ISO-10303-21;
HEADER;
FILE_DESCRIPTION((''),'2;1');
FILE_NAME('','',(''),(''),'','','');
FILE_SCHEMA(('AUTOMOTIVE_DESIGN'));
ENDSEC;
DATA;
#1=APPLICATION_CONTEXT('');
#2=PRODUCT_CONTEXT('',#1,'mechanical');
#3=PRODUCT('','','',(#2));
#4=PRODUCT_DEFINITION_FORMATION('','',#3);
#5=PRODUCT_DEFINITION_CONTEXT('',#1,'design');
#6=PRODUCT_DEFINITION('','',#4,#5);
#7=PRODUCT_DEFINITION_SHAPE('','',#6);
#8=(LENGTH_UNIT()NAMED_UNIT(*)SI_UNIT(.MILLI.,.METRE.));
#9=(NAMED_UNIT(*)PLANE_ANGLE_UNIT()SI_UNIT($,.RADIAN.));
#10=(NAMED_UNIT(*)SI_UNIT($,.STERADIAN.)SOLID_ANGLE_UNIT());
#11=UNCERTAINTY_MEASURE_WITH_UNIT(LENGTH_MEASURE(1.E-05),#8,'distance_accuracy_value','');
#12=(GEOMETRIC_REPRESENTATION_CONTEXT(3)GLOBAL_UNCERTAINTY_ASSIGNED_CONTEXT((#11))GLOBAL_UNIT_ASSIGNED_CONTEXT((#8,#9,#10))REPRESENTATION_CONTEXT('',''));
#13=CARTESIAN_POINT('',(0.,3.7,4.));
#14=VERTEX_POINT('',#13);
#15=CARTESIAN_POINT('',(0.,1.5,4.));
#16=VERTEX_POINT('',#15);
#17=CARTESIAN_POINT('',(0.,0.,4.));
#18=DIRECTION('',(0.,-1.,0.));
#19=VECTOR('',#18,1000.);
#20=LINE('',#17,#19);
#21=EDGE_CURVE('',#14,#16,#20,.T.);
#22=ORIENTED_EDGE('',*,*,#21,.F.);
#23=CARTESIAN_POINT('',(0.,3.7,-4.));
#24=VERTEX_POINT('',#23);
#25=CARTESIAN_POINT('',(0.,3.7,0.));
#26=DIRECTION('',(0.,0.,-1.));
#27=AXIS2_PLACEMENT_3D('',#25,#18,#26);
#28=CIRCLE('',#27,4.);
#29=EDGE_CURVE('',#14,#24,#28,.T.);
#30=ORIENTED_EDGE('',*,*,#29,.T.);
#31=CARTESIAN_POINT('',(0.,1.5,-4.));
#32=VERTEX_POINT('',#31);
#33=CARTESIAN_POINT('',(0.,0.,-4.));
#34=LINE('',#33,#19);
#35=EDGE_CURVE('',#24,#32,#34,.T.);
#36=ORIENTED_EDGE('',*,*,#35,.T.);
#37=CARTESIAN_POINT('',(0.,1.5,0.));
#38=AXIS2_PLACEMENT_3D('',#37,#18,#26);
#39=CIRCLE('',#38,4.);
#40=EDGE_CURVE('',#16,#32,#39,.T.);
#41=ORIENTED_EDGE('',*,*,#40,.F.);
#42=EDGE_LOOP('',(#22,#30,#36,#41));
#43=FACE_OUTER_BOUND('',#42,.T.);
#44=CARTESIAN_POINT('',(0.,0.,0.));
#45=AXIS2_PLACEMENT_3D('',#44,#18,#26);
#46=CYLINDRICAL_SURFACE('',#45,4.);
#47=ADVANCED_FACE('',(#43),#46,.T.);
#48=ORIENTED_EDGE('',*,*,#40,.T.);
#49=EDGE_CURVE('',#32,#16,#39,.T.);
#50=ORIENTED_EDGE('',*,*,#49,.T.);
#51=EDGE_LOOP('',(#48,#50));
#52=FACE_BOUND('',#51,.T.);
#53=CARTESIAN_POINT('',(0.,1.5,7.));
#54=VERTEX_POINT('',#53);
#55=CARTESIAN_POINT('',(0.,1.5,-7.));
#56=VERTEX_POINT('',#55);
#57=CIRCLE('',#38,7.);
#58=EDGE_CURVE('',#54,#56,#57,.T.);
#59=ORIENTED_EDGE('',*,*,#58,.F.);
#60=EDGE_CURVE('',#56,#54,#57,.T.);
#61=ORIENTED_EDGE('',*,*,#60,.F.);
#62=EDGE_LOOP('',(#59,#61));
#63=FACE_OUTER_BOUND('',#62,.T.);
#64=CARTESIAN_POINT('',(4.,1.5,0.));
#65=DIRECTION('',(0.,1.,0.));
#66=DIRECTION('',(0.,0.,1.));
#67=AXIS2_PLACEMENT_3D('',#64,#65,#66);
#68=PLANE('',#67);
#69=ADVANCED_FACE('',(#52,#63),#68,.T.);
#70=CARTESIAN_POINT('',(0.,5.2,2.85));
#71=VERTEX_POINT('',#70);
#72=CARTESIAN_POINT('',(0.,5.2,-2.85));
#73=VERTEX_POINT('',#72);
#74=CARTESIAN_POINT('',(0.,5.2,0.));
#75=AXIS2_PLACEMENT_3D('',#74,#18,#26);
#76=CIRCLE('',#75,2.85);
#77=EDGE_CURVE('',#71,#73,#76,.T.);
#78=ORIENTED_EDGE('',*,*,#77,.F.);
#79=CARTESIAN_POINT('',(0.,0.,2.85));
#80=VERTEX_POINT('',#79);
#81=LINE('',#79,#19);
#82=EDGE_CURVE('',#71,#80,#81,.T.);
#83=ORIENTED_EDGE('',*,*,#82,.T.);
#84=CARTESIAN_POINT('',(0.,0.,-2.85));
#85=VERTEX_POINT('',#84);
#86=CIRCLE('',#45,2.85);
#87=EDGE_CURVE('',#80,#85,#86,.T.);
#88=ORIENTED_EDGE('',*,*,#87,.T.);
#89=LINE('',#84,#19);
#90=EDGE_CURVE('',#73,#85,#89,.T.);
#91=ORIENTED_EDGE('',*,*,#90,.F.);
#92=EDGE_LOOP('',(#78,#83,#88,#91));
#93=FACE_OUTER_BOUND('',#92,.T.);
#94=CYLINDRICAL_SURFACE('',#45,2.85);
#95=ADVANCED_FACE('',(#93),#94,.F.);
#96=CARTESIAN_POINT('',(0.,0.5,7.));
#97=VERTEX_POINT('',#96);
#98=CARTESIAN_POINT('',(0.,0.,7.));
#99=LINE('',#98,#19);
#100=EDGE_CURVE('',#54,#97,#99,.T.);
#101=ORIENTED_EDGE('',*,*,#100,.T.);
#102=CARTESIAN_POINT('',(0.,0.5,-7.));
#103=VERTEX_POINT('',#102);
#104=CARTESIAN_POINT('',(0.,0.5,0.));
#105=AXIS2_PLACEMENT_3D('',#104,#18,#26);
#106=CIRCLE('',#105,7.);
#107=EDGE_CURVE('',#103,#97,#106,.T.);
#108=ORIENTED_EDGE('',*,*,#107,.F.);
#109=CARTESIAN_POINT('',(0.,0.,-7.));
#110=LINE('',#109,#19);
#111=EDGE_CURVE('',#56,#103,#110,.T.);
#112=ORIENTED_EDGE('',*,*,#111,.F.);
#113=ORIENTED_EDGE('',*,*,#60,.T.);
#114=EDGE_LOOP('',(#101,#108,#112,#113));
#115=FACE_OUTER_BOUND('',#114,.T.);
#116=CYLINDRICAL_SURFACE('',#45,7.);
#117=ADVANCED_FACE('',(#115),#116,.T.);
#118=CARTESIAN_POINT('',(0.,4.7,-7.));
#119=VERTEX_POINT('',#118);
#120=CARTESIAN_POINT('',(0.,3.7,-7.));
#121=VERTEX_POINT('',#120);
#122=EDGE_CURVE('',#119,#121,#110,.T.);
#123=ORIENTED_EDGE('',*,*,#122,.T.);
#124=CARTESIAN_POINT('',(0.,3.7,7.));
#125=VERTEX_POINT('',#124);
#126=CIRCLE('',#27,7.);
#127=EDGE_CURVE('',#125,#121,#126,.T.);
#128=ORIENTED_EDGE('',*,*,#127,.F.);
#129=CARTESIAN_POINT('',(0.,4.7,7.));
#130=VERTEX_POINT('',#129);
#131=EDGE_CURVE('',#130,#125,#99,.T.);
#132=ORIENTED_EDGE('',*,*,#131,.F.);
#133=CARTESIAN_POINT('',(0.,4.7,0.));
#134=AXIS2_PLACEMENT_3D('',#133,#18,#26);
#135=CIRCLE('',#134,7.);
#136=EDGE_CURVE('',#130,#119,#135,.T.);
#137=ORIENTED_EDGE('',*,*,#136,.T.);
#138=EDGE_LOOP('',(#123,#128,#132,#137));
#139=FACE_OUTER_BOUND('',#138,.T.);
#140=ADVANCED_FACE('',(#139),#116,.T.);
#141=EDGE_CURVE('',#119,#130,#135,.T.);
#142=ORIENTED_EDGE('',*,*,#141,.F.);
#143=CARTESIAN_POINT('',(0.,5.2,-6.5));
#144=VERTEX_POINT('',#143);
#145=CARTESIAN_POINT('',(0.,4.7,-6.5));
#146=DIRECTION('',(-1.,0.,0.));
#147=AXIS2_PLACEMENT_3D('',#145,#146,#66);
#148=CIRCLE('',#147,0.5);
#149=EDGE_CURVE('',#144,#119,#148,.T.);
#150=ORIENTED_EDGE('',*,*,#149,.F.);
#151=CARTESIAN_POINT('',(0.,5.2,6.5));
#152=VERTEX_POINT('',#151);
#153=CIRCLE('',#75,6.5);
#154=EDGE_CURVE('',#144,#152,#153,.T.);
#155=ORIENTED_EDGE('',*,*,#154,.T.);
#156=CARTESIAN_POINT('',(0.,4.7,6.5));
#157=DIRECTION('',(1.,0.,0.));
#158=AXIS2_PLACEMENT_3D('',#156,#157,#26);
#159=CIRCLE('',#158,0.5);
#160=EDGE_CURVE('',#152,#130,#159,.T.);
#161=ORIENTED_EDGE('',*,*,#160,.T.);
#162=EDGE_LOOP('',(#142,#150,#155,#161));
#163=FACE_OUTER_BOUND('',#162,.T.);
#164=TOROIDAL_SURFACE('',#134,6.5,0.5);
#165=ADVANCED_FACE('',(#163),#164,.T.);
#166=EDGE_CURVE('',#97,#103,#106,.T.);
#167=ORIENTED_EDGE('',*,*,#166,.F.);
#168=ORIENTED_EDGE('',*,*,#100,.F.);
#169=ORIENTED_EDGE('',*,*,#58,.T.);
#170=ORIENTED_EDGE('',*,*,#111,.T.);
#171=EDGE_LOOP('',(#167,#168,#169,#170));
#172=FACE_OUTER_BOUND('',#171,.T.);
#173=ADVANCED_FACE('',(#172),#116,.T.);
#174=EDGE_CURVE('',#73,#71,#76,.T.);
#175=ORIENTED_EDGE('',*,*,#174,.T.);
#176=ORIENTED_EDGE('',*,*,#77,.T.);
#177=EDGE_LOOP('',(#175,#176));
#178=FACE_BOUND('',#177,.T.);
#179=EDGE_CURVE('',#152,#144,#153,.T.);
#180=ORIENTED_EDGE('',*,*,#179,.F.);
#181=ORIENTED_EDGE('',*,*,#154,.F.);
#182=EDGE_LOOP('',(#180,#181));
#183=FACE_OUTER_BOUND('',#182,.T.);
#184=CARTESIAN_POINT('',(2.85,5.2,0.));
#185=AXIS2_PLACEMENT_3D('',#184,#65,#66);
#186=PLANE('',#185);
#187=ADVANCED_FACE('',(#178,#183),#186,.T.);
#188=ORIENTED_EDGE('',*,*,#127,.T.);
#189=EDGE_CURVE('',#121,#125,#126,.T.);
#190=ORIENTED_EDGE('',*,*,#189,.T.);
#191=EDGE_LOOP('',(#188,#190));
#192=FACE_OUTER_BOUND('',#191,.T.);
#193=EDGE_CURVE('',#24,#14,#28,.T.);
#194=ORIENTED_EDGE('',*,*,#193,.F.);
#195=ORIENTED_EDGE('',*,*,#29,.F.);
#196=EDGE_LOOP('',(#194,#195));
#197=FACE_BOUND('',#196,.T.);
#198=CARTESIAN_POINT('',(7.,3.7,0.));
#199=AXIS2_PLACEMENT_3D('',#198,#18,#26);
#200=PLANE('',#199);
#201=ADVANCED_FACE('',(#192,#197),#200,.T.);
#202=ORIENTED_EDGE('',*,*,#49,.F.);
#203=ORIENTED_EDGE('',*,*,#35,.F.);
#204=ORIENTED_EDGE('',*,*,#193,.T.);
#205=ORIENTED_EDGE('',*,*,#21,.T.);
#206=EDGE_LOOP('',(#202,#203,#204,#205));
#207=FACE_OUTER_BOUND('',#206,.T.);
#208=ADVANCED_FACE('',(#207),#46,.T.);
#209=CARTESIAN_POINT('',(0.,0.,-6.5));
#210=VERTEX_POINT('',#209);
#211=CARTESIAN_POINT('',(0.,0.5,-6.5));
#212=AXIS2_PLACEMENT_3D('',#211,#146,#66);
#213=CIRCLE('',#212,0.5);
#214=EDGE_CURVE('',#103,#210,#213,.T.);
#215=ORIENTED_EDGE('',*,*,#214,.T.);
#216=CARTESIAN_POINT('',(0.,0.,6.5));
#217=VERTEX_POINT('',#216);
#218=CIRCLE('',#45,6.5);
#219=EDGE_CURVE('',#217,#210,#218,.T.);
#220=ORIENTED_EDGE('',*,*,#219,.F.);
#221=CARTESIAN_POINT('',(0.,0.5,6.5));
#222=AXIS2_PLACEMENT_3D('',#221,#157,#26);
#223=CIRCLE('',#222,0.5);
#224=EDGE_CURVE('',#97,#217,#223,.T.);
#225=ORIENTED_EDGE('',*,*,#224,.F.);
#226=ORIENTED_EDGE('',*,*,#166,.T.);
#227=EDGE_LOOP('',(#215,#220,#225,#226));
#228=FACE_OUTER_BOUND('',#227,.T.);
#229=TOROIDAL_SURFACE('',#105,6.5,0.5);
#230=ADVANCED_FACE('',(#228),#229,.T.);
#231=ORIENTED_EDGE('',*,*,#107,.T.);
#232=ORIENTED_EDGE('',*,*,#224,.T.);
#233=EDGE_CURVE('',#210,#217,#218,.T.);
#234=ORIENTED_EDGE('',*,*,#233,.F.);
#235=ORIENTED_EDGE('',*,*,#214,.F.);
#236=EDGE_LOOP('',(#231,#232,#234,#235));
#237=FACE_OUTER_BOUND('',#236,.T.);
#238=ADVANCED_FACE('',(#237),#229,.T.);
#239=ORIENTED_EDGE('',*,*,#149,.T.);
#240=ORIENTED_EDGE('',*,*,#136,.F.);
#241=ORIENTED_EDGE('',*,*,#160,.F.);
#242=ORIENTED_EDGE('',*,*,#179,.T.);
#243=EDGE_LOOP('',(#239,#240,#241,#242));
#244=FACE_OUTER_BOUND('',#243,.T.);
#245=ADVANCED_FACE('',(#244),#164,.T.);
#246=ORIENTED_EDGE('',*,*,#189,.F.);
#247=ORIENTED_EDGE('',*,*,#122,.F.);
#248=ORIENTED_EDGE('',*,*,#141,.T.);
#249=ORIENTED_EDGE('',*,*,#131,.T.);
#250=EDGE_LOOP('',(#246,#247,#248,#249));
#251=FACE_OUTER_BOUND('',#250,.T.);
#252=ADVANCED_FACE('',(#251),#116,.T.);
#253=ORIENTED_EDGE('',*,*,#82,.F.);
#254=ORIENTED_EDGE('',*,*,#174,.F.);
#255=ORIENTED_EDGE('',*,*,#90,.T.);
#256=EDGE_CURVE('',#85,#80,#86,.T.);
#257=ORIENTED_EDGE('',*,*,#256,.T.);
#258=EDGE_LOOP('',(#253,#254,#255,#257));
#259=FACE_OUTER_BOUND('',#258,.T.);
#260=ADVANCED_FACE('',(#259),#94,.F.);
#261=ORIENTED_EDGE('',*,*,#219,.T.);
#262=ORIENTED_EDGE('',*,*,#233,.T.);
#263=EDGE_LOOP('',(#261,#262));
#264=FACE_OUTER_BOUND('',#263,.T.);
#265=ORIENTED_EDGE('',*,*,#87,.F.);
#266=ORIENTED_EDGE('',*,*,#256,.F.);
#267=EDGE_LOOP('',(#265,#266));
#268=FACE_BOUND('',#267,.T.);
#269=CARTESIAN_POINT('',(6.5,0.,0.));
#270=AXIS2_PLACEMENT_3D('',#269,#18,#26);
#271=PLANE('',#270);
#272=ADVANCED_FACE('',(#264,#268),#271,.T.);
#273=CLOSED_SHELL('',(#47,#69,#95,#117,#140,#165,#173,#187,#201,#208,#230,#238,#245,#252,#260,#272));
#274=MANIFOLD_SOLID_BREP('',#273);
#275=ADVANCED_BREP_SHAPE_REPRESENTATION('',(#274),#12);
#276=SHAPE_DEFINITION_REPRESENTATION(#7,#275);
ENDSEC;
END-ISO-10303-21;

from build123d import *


with BuildPart() as part:
    # 草图1 → 旋转1 (revolve)
    with BuildSketch(Plane.XY, mode=Mode.PRIVATE) as revolve_1_sk:
        with BuildLine():
            Line((2.85, 5.2), (6.5, 5.2))
            ThreePointArc((6.5, 5.2), (6.853553391, 5.053553391), (7, 4.7))
            Line((7, 4.7), (7, 3.7))
            Line((7, 3.7), (4, 3.7))
            Line((4, 3.7), (4, 1.5))
            Line((4, 1.5), (7, 1.5))
            Line((7, 1.5), (7, 0.5))
            ThreePointArc((7, 0.5), (6.853553391, 0.146446609), (6.5, 0))
            Line((6.5, 0), (2.85, 0))
            Line((2.85, 0), (2.85, 5.2))
        make_face()
    revolve(revolve_1_sk.sketch.rotate(Axis((0, 0, 0), (0, 1, 0)), 90), axis=Axis((0, 0, 0), (0, 1, 0)))


solid = part.part
